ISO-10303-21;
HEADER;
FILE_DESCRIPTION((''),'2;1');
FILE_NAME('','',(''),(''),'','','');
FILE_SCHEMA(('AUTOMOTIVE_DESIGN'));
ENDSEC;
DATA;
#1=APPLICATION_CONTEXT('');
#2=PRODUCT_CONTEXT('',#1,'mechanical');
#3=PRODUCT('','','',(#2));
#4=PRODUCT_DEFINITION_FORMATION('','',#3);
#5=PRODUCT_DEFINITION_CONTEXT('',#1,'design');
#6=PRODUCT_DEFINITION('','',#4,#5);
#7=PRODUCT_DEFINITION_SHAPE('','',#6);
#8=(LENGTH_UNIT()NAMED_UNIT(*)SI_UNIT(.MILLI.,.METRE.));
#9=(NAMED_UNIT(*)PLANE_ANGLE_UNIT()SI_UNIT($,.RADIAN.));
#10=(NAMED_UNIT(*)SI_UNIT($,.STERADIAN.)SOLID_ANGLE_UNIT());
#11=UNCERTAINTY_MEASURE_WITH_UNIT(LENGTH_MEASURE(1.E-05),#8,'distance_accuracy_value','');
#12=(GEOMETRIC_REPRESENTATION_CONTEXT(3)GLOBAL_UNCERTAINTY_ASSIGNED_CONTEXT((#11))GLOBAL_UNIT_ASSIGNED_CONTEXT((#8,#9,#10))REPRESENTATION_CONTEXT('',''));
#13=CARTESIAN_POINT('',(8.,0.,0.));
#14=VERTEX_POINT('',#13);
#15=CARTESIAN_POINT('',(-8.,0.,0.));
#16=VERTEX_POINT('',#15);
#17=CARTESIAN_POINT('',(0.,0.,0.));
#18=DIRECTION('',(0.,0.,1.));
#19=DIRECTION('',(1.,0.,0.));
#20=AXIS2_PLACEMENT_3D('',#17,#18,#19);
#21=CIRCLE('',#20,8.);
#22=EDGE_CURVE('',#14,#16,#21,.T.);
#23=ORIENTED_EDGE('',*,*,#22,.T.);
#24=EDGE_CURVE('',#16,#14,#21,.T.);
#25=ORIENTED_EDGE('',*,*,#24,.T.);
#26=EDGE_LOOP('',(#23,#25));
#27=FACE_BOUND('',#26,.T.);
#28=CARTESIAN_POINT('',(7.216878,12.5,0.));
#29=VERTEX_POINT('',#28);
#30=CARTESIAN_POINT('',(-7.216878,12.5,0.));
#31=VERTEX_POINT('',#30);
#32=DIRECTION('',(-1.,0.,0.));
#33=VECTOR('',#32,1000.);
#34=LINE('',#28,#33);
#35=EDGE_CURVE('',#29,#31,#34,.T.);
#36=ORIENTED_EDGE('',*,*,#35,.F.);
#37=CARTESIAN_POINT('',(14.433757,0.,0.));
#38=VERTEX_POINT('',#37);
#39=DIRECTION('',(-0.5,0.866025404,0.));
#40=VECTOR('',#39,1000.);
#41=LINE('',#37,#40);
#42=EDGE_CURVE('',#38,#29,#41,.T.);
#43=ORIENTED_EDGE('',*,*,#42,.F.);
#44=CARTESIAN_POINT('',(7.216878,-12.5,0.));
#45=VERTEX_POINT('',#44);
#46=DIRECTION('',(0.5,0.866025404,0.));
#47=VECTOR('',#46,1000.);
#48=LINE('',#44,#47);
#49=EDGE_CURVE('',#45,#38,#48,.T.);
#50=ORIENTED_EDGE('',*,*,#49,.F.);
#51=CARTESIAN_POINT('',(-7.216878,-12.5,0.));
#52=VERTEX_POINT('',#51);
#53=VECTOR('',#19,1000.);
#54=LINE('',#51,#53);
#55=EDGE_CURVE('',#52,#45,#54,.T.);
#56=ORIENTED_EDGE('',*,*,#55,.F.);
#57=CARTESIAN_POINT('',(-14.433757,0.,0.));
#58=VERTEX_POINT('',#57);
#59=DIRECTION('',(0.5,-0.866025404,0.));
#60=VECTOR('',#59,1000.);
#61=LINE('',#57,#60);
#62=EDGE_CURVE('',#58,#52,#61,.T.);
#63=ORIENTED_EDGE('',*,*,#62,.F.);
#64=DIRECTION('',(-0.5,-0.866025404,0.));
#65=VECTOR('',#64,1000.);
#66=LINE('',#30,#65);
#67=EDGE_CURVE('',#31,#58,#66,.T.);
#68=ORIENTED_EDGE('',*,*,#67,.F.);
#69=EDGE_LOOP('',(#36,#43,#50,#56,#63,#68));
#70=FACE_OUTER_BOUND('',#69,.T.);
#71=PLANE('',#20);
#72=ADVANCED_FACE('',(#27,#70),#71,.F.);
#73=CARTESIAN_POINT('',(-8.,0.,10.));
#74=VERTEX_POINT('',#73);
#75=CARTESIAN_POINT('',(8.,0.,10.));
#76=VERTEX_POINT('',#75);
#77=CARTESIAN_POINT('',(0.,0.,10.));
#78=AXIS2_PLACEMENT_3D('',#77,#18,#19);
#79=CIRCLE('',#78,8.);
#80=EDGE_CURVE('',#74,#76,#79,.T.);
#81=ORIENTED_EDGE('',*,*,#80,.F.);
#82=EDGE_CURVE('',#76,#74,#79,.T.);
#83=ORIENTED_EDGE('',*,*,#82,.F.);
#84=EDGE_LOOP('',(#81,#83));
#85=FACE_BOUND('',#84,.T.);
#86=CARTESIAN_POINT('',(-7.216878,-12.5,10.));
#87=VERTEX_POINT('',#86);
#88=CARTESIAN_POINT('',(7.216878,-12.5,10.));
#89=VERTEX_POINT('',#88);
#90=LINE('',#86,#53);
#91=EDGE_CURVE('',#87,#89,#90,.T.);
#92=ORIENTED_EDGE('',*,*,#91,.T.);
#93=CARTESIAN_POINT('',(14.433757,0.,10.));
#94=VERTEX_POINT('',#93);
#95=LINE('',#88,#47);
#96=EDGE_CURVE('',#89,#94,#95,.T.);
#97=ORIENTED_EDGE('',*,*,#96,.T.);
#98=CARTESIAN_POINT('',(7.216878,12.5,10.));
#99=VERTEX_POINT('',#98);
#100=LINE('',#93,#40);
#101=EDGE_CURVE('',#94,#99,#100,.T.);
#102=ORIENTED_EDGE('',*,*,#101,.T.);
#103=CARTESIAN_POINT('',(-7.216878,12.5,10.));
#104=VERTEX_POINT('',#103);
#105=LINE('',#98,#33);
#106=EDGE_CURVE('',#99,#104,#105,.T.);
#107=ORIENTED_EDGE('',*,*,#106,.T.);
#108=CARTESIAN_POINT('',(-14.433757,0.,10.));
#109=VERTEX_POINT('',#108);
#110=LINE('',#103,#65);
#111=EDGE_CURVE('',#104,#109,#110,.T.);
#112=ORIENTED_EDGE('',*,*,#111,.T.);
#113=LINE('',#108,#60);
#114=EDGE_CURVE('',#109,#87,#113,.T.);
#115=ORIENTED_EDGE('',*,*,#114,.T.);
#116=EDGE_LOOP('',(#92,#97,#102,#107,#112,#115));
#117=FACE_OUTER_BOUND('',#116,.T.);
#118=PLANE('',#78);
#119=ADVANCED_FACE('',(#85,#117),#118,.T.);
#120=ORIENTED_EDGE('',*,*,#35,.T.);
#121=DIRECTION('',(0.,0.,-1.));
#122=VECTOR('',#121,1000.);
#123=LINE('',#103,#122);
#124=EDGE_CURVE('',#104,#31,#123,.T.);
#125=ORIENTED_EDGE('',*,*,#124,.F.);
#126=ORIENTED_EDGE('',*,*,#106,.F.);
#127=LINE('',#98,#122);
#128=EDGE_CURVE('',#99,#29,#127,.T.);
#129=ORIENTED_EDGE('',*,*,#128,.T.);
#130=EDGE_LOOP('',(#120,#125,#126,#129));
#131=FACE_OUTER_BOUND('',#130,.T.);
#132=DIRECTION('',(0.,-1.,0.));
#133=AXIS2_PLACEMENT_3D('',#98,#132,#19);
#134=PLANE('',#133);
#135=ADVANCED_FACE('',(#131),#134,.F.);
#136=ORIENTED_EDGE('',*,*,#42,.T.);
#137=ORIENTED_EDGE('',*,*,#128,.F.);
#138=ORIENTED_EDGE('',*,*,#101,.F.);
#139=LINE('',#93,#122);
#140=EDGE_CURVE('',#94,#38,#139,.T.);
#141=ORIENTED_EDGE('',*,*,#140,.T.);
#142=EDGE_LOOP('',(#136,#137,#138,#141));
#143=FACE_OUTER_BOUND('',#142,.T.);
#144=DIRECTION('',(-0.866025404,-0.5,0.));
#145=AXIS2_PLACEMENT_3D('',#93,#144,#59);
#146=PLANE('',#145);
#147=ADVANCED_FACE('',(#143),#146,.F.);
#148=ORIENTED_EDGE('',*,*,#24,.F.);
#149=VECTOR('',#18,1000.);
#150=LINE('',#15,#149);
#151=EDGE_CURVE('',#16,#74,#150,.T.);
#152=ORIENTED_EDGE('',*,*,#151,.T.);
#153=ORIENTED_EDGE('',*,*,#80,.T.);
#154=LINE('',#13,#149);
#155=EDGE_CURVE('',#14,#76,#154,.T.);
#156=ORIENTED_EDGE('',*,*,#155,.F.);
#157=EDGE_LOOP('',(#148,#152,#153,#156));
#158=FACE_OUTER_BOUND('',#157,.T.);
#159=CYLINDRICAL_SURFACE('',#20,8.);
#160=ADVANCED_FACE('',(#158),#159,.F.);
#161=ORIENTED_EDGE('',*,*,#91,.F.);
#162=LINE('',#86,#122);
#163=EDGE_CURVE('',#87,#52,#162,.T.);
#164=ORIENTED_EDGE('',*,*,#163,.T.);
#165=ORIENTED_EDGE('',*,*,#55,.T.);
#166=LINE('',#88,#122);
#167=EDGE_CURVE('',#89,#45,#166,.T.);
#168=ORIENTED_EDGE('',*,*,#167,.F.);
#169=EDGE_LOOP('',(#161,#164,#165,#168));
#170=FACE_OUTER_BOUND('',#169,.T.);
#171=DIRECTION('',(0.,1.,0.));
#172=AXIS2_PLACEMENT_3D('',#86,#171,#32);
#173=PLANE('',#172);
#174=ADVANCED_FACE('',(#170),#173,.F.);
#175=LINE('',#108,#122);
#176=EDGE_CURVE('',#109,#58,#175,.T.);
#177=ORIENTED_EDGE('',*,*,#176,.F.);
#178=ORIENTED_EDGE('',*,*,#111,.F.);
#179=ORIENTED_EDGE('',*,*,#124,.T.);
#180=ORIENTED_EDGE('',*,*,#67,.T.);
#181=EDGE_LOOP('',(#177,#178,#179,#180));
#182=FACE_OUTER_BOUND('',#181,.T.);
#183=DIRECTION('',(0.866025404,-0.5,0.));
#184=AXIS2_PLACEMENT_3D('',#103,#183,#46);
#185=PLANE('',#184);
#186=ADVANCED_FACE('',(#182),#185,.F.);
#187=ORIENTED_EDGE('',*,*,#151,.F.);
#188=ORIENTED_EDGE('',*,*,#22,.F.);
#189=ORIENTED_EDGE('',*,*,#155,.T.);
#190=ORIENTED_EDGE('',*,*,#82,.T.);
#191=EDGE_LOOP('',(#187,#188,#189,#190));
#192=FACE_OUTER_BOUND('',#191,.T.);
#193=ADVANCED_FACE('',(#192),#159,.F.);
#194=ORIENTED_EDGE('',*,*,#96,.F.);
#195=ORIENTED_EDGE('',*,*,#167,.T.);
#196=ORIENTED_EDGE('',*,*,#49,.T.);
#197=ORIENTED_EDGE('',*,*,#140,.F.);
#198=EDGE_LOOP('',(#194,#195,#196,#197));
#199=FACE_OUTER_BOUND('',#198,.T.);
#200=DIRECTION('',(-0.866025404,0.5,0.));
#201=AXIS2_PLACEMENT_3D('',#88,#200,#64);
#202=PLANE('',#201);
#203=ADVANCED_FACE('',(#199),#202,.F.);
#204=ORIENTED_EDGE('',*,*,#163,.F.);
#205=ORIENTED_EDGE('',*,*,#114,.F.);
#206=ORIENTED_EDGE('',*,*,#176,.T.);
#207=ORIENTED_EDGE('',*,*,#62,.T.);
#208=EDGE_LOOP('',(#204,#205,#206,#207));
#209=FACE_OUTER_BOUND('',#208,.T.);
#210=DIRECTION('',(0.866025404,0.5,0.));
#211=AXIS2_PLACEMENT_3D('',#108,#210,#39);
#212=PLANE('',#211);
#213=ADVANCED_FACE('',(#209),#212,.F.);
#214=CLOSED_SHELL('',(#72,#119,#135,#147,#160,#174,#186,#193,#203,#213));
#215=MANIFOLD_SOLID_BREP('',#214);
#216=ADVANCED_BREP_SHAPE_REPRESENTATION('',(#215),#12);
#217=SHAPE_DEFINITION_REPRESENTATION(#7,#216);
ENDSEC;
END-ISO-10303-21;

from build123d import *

# Parameters (mm, degrees)
HEX_BODY_25AF_X10_DEPTH = 10
BORE_SKETCH_16_R        = 8
BORE_16_DEPTH           = 10


with BuildPart() as part:
    # Hex Profile Sketch 25AF → Hex Body 25AF x10 (new body)
    with BuildSketch(Plane.XY):
        Polygon((14.43375673, 0), (7.216878365, 12.5), (-7.216878365, 12.5), (-14.43375673, 0), (-7.216878365, -12.5), (7.216878365, -12.5), align=None)
    extrude(amount=HEX_BODY_25AF_X10_DEPTH)

    # Bore Sketch Ø16 → Bore Ø16 (cut)
    with BuildSketch(Plane.XY.offset(10)):
        Circle(BORE_SKETCH_16_R)
    extrude(amount=-BORE_16_DEPTH, mode=Mode.SUBTRACT)


solid = part.part
